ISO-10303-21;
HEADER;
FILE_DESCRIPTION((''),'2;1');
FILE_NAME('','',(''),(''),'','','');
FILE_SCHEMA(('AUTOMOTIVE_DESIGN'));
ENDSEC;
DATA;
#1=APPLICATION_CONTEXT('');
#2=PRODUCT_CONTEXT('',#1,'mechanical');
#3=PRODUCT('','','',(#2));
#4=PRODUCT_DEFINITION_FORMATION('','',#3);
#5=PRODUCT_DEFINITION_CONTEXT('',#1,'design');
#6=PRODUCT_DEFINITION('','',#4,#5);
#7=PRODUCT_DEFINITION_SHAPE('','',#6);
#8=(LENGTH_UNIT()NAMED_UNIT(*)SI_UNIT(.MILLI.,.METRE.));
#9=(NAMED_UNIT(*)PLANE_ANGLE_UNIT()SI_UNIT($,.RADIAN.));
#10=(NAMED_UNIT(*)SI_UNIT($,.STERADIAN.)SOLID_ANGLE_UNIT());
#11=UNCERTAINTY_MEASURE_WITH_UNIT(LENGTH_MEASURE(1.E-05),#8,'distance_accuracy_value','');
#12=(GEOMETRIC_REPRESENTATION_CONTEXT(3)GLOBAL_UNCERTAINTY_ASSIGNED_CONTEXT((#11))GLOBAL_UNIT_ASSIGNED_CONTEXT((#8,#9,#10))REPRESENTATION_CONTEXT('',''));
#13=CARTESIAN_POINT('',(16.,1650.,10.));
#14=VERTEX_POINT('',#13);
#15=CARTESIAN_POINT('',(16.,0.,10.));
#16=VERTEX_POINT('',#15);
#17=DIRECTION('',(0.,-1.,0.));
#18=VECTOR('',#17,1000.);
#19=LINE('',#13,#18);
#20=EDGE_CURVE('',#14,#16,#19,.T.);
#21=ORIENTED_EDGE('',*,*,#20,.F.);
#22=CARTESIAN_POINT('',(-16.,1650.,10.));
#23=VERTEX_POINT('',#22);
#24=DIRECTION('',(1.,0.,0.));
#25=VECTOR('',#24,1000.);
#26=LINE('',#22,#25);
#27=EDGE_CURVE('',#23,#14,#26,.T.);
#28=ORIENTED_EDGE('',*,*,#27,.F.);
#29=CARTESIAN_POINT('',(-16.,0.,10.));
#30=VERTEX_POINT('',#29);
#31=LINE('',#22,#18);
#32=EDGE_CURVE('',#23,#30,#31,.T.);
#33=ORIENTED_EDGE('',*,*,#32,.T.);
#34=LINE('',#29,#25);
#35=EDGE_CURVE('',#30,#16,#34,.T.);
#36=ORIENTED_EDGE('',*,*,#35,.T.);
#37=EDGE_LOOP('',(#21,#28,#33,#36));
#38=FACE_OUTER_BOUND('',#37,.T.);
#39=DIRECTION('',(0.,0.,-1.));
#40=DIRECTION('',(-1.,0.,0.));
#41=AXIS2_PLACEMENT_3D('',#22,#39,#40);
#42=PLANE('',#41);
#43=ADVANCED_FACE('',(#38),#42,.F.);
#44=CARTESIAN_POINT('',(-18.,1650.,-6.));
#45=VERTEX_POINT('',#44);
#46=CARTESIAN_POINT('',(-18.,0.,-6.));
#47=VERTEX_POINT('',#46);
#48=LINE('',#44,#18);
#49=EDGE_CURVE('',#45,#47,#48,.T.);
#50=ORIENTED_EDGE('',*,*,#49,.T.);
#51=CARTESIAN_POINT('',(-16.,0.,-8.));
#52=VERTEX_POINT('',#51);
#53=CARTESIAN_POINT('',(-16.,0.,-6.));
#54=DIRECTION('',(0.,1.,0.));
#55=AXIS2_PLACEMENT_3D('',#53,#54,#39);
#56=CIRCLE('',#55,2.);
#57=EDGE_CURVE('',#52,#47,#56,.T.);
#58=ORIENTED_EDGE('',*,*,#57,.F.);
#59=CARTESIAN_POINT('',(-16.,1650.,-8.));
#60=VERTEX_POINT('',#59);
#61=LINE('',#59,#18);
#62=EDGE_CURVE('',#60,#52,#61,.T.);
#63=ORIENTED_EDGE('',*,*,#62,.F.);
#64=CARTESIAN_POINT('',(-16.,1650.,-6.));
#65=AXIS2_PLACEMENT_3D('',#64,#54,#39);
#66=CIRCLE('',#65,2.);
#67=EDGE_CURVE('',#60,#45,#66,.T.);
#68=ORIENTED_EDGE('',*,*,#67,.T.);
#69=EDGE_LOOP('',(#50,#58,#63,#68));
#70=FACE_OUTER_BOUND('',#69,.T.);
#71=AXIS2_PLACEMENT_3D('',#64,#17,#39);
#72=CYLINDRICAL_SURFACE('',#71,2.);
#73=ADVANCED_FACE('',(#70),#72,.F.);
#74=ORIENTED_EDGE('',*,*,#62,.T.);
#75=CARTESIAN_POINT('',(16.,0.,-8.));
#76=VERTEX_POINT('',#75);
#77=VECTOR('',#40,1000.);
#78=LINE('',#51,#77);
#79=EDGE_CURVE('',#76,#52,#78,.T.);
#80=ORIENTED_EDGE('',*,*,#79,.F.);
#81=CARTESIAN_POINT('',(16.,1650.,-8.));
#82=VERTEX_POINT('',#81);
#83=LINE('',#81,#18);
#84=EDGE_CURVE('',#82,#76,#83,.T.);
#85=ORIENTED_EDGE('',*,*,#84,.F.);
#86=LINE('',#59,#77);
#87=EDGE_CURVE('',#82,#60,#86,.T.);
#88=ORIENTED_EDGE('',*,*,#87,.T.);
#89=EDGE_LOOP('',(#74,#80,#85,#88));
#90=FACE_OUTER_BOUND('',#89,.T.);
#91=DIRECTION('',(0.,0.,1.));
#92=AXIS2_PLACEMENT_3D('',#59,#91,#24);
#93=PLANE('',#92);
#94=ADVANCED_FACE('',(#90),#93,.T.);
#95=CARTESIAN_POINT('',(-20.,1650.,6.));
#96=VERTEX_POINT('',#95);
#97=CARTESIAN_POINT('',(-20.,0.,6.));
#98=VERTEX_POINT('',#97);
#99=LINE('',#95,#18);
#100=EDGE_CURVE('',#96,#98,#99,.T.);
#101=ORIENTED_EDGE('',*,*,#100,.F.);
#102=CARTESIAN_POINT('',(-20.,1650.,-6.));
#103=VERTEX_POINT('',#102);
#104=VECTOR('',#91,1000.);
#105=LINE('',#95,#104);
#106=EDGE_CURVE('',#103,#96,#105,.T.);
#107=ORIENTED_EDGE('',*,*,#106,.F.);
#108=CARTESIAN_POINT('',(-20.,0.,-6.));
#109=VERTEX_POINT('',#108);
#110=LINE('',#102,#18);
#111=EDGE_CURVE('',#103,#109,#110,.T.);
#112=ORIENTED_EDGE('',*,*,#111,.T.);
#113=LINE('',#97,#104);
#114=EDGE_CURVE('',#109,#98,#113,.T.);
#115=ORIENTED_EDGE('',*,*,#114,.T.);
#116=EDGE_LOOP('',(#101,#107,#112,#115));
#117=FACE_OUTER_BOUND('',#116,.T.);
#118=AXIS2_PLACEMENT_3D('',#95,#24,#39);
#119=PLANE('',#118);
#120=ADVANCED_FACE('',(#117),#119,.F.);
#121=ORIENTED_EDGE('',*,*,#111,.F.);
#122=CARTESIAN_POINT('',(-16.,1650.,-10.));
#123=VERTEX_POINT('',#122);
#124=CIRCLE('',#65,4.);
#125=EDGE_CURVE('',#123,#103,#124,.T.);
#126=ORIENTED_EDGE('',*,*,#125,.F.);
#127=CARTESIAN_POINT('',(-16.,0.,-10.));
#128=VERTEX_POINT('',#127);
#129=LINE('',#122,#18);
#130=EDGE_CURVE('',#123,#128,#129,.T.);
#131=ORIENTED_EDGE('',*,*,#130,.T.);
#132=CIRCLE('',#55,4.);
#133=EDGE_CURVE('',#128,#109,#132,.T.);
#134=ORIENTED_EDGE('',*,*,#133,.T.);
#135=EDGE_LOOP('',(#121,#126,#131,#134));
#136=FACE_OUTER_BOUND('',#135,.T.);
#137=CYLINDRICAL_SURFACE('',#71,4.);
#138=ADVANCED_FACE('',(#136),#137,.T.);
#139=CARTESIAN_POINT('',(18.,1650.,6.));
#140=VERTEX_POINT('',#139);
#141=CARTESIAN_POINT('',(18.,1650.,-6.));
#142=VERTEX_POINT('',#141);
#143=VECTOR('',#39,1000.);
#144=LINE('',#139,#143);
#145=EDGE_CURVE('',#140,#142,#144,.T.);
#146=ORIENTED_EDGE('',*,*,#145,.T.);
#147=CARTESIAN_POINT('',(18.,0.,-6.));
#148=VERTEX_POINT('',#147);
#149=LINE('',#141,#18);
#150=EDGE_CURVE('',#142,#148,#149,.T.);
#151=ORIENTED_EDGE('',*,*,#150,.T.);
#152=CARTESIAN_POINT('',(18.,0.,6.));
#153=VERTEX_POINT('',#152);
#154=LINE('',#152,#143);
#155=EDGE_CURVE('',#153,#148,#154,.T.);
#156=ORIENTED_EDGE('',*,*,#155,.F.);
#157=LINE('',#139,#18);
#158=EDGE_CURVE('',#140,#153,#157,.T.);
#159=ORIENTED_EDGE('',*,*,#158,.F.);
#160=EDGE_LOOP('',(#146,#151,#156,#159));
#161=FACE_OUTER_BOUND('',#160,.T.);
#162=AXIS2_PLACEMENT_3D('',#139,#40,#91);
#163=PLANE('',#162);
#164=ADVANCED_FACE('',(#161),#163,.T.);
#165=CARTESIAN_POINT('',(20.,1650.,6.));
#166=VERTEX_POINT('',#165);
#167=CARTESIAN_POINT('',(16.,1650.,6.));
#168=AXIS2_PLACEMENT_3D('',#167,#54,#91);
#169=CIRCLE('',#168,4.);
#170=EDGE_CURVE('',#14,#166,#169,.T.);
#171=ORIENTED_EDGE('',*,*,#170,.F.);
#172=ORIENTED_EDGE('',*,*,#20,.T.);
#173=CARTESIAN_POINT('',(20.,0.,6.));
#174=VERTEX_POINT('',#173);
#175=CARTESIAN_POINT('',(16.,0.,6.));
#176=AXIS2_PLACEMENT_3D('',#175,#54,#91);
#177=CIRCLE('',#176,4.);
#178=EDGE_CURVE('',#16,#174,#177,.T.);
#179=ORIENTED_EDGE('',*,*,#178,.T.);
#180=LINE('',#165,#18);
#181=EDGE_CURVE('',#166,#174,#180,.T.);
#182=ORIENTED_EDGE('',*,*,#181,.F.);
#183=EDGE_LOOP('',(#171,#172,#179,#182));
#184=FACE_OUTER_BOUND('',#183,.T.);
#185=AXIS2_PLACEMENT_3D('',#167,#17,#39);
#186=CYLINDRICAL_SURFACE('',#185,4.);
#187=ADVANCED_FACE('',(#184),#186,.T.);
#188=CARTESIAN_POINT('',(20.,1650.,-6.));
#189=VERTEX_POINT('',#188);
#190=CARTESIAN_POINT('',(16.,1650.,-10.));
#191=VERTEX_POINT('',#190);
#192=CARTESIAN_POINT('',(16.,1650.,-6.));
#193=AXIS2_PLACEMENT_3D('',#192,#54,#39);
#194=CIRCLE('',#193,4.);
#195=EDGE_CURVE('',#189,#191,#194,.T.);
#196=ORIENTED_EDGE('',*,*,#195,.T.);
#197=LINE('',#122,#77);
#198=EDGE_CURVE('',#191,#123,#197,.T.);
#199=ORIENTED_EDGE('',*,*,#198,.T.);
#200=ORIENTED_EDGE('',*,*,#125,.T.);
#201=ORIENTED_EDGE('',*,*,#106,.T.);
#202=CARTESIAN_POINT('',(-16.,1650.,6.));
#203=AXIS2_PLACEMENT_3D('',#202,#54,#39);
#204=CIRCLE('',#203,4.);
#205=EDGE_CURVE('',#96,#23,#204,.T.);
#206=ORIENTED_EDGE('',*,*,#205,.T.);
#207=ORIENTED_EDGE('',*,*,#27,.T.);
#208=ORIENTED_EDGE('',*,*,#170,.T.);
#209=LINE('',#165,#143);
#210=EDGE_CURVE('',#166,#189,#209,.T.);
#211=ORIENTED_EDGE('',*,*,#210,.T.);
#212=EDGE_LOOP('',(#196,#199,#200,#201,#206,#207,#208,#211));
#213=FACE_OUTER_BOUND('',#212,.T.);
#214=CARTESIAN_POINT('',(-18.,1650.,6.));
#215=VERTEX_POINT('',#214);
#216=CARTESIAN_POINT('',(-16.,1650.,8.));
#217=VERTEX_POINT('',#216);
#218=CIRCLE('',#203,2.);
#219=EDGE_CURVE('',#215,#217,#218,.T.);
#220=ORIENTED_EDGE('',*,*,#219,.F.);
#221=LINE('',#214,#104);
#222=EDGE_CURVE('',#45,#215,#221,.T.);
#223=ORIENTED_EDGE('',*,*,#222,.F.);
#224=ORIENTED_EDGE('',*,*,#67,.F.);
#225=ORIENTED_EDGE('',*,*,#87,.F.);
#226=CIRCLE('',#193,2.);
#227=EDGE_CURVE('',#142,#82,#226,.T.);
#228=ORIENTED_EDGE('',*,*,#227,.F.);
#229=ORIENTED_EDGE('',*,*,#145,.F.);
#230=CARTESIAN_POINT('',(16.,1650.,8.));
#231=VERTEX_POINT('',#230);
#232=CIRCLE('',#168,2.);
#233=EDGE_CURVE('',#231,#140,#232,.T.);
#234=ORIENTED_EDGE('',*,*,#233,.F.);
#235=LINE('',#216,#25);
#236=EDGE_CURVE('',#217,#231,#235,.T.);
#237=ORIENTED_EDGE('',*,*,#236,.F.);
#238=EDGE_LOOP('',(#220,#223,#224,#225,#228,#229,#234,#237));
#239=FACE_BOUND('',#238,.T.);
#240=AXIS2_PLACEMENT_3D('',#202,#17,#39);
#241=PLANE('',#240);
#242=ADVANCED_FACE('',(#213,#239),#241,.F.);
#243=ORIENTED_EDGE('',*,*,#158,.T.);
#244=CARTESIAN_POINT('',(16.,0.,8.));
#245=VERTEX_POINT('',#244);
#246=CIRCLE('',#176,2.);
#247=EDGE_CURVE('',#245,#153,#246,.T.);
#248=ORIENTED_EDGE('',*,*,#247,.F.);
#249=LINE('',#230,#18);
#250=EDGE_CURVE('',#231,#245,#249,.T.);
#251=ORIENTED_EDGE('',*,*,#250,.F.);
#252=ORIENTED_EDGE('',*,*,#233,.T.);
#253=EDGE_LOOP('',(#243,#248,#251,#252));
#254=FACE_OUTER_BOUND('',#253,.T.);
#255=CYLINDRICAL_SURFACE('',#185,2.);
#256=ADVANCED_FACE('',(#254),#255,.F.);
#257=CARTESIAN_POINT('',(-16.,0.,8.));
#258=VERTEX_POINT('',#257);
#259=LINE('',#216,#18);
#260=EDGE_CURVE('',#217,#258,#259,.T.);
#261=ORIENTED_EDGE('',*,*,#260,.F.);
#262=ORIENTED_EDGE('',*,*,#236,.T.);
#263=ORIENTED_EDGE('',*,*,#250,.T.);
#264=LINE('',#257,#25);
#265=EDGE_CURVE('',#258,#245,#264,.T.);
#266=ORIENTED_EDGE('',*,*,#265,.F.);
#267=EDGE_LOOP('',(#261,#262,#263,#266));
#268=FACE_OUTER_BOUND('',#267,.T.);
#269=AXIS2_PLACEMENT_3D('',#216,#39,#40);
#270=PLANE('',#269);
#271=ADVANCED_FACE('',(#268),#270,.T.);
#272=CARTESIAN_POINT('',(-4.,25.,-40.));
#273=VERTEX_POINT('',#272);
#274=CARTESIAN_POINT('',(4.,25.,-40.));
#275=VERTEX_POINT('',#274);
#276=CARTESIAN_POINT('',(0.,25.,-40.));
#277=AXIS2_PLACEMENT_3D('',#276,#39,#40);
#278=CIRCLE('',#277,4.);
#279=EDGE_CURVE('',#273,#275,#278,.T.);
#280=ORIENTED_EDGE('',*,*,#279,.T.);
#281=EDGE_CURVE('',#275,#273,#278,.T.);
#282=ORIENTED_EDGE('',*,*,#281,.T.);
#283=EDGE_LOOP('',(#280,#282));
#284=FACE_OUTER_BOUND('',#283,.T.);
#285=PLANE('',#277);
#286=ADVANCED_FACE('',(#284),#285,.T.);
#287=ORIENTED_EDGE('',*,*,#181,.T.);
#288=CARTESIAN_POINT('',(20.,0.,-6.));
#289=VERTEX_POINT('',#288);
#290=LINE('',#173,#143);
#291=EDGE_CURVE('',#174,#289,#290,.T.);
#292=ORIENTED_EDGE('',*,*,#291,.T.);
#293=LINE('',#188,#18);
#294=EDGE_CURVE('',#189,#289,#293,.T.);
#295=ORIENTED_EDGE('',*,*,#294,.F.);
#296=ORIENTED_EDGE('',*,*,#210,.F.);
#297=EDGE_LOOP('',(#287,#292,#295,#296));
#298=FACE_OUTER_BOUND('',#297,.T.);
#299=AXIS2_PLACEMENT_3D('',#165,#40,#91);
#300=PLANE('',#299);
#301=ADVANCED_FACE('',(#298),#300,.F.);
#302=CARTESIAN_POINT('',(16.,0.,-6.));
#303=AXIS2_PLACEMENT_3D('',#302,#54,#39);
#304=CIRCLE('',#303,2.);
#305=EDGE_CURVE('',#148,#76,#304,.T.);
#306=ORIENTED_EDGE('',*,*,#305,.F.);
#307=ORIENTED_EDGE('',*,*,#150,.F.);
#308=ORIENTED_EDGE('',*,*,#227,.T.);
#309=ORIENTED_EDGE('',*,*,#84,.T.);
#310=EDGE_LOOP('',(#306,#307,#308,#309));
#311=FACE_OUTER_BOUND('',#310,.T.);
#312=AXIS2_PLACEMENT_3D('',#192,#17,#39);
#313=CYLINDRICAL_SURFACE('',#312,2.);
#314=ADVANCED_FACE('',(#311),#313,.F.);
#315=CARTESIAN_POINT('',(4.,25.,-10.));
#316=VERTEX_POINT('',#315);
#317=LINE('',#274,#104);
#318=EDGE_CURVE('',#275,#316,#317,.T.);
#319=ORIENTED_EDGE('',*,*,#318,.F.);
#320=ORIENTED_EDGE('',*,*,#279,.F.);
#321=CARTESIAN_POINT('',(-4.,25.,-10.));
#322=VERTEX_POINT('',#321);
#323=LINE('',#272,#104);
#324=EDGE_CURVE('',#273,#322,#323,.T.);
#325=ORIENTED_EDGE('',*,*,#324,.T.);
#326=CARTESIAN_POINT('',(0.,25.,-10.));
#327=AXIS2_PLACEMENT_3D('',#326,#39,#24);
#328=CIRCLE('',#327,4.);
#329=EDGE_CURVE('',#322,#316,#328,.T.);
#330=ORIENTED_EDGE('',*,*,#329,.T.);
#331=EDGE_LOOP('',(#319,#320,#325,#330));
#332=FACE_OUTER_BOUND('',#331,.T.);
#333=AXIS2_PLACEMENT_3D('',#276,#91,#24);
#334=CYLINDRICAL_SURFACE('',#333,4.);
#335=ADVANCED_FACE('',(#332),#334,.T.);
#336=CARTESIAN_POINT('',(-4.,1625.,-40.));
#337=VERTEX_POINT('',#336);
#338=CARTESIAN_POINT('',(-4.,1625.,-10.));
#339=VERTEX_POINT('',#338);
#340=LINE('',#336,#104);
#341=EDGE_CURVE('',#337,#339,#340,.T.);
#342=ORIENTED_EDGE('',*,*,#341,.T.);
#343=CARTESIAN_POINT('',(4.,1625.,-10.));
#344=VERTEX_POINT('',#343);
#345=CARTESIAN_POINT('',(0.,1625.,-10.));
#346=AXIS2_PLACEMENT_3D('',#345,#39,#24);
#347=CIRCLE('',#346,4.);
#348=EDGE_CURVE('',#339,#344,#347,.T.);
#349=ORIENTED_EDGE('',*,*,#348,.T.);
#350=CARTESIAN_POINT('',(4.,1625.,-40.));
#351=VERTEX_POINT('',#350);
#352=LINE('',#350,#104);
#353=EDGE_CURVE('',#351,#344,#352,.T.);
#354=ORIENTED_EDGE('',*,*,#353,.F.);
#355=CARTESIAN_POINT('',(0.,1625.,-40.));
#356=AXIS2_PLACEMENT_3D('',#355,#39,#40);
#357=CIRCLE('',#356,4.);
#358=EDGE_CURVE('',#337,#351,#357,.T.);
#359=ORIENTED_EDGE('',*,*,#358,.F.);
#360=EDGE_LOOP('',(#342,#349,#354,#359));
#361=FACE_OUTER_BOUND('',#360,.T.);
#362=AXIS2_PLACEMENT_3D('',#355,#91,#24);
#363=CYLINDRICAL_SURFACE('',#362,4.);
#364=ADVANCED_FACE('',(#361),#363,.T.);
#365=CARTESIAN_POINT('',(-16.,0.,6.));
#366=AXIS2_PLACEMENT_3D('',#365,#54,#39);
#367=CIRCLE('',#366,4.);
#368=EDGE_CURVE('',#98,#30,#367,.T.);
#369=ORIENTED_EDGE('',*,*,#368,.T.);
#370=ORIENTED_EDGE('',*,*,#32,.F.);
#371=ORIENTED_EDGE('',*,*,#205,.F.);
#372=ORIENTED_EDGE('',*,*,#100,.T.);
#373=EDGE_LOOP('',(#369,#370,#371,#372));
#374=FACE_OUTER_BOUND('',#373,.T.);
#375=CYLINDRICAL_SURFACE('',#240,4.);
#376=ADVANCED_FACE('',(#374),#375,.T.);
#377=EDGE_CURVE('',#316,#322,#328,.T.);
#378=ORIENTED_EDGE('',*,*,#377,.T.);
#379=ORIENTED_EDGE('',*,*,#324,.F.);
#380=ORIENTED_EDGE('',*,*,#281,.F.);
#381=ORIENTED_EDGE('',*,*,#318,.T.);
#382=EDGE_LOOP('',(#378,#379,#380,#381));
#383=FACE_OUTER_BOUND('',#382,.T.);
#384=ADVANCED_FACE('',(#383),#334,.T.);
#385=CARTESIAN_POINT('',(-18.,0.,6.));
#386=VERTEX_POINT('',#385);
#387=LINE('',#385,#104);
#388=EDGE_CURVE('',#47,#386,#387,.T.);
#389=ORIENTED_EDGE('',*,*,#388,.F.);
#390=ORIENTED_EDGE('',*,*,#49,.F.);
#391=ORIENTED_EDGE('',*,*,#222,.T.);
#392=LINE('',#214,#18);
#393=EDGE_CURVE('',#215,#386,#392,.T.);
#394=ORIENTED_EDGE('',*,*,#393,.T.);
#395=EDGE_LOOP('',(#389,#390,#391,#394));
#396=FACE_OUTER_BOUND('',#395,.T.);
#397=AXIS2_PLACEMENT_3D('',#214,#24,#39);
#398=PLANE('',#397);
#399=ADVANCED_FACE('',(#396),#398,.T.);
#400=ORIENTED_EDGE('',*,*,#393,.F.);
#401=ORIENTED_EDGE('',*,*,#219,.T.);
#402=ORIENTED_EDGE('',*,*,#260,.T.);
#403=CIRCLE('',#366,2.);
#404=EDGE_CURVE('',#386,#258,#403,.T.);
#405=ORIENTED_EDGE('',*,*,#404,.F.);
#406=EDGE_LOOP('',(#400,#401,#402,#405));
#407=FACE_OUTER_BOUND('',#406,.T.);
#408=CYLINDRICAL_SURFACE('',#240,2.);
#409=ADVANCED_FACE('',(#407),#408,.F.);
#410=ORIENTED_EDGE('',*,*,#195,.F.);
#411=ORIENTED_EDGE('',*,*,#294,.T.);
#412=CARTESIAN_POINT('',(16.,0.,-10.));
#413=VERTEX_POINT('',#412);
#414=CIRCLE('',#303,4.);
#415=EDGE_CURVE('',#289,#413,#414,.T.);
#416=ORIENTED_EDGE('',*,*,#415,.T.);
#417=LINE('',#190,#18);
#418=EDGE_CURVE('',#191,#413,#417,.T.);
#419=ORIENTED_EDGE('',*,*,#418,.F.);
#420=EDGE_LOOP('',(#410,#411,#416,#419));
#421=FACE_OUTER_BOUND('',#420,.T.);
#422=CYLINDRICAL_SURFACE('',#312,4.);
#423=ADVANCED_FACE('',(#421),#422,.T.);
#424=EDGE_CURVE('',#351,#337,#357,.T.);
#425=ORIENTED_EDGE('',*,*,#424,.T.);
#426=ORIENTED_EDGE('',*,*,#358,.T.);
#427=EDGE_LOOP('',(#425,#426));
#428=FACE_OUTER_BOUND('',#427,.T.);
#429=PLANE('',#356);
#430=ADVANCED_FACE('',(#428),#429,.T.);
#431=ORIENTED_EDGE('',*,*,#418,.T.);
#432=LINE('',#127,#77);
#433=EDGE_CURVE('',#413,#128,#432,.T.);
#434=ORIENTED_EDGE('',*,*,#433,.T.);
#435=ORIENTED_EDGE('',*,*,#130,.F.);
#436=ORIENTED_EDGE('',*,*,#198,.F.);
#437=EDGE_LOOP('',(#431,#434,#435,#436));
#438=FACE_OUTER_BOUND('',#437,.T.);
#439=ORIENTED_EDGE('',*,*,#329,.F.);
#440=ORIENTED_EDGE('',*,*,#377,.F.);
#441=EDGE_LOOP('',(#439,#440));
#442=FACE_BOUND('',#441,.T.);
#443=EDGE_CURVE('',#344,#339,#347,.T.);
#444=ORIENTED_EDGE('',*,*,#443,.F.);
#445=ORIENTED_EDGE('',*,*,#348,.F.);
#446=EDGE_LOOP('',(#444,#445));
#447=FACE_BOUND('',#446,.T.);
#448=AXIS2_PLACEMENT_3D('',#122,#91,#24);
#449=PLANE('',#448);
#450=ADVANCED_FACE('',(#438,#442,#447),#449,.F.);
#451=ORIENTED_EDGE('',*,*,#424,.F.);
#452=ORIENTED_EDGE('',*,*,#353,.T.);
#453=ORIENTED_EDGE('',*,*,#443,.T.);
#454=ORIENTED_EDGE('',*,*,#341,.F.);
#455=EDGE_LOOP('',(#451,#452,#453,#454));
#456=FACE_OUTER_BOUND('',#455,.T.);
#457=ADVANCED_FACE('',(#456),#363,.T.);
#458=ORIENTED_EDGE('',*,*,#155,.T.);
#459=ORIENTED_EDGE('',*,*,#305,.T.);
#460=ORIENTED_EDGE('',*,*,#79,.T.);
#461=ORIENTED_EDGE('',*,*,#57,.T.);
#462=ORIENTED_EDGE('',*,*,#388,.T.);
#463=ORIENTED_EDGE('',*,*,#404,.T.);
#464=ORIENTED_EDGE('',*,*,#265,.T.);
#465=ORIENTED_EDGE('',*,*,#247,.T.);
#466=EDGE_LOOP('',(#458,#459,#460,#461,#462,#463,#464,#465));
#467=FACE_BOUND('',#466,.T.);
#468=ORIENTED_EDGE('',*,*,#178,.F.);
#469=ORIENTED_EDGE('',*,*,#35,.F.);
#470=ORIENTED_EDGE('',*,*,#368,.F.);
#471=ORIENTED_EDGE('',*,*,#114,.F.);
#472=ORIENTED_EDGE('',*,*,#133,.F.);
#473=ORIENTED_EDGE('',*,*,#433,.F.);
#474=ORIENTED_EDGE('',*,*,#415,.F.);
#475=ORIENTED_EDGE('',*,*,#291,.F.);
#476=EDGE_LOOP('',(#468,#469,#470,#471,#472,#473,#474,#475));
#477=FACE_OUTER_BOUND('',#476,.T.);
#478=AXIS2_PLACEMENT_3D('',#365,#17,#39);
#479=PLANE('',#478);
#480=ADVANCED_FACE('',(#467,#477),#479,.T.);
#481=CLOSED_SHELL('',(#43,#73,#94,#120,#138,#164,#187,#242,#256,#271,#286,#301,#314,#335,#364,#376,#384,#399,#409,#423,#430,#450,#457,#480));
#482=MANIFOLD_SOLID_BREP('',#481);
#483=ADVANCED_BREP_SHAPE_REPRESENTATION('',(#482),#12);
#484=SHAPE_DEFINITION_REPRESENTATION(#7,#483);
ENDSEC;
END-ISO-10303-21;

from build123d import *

# Parameters (mm, degrees)
EXTRUDE_1_DEPTH = 1650
SKETCH_2_R      = 4
EXTRUDE_2_DEPTH = 30


with BuildPart() as part:
    # 草图1 → 凸台-拉伸1 (new body)
    with BuildSketch(Plane(origin=(0, 0, 0), x_dir=(1, 0, 0), z_dir=(0, 1, 0))):
        with BuildLine():
            Line((-16, -10), (16, -10))
            ThreePointArc((16, -10), (18.828427125, -8.828427125), (20, -6))
            Line((20, -6), (20, 6))
            ThreePointArc((20, 6), (18.828427125, 8.828427125), (16, 10))
            Line((16, 10), (-16, 10))
            ThreePointArc((-16, 10), (-18.828427125, 8.828427125), (-20, 6))
            Line((-20, 6), (-20, -6))
            ThreePointArc((-20, -6), (-18.828427125, -8.828427125), (-16, -10))
        make_face()
        with BuildLine():
            Line((-16, -8), (16, -8))
            ThreePointArc((16, -8), (17.414213562, -7.414213562), (18, -6))
            Line((18, -6), (18, 6))
            ThreePointArc((18, 6), (17.414213562, 7.414213562), (16, 8))
            Line((16, 8), (-16, 8))
            ThreePointArc((-16, 8), (-17.414213562, 7.414213562), (-18, 6))
            Line((-18, 6), (-18, -6))
            ThreePointArc((-18, -6), (-17.414213562, -7.414213562), (-16, -8))
        make_face(mode=Mode.SUBTRACT)
    extrude(amount=EXTRUDE_1_DEPTH)

    # 草图2 → 凸台-拉伸2 (add)
    with BuildSketch(Plane(origin=(0, 0, -10), x_dir=(-1, 0, 0), z_dir=(0, 0, -1))):
        with Locations(Location((0, 1625, 0), (0, 0, 180))):
            Circle(SKETCH_2_R)
        with Locations(Location((0, 25, 0), (0, 0, 180))):
            Circle(SKETCH_2_R)
    extrude(amount=EXTRUDE_2_DEPTH)


solid = part.part
